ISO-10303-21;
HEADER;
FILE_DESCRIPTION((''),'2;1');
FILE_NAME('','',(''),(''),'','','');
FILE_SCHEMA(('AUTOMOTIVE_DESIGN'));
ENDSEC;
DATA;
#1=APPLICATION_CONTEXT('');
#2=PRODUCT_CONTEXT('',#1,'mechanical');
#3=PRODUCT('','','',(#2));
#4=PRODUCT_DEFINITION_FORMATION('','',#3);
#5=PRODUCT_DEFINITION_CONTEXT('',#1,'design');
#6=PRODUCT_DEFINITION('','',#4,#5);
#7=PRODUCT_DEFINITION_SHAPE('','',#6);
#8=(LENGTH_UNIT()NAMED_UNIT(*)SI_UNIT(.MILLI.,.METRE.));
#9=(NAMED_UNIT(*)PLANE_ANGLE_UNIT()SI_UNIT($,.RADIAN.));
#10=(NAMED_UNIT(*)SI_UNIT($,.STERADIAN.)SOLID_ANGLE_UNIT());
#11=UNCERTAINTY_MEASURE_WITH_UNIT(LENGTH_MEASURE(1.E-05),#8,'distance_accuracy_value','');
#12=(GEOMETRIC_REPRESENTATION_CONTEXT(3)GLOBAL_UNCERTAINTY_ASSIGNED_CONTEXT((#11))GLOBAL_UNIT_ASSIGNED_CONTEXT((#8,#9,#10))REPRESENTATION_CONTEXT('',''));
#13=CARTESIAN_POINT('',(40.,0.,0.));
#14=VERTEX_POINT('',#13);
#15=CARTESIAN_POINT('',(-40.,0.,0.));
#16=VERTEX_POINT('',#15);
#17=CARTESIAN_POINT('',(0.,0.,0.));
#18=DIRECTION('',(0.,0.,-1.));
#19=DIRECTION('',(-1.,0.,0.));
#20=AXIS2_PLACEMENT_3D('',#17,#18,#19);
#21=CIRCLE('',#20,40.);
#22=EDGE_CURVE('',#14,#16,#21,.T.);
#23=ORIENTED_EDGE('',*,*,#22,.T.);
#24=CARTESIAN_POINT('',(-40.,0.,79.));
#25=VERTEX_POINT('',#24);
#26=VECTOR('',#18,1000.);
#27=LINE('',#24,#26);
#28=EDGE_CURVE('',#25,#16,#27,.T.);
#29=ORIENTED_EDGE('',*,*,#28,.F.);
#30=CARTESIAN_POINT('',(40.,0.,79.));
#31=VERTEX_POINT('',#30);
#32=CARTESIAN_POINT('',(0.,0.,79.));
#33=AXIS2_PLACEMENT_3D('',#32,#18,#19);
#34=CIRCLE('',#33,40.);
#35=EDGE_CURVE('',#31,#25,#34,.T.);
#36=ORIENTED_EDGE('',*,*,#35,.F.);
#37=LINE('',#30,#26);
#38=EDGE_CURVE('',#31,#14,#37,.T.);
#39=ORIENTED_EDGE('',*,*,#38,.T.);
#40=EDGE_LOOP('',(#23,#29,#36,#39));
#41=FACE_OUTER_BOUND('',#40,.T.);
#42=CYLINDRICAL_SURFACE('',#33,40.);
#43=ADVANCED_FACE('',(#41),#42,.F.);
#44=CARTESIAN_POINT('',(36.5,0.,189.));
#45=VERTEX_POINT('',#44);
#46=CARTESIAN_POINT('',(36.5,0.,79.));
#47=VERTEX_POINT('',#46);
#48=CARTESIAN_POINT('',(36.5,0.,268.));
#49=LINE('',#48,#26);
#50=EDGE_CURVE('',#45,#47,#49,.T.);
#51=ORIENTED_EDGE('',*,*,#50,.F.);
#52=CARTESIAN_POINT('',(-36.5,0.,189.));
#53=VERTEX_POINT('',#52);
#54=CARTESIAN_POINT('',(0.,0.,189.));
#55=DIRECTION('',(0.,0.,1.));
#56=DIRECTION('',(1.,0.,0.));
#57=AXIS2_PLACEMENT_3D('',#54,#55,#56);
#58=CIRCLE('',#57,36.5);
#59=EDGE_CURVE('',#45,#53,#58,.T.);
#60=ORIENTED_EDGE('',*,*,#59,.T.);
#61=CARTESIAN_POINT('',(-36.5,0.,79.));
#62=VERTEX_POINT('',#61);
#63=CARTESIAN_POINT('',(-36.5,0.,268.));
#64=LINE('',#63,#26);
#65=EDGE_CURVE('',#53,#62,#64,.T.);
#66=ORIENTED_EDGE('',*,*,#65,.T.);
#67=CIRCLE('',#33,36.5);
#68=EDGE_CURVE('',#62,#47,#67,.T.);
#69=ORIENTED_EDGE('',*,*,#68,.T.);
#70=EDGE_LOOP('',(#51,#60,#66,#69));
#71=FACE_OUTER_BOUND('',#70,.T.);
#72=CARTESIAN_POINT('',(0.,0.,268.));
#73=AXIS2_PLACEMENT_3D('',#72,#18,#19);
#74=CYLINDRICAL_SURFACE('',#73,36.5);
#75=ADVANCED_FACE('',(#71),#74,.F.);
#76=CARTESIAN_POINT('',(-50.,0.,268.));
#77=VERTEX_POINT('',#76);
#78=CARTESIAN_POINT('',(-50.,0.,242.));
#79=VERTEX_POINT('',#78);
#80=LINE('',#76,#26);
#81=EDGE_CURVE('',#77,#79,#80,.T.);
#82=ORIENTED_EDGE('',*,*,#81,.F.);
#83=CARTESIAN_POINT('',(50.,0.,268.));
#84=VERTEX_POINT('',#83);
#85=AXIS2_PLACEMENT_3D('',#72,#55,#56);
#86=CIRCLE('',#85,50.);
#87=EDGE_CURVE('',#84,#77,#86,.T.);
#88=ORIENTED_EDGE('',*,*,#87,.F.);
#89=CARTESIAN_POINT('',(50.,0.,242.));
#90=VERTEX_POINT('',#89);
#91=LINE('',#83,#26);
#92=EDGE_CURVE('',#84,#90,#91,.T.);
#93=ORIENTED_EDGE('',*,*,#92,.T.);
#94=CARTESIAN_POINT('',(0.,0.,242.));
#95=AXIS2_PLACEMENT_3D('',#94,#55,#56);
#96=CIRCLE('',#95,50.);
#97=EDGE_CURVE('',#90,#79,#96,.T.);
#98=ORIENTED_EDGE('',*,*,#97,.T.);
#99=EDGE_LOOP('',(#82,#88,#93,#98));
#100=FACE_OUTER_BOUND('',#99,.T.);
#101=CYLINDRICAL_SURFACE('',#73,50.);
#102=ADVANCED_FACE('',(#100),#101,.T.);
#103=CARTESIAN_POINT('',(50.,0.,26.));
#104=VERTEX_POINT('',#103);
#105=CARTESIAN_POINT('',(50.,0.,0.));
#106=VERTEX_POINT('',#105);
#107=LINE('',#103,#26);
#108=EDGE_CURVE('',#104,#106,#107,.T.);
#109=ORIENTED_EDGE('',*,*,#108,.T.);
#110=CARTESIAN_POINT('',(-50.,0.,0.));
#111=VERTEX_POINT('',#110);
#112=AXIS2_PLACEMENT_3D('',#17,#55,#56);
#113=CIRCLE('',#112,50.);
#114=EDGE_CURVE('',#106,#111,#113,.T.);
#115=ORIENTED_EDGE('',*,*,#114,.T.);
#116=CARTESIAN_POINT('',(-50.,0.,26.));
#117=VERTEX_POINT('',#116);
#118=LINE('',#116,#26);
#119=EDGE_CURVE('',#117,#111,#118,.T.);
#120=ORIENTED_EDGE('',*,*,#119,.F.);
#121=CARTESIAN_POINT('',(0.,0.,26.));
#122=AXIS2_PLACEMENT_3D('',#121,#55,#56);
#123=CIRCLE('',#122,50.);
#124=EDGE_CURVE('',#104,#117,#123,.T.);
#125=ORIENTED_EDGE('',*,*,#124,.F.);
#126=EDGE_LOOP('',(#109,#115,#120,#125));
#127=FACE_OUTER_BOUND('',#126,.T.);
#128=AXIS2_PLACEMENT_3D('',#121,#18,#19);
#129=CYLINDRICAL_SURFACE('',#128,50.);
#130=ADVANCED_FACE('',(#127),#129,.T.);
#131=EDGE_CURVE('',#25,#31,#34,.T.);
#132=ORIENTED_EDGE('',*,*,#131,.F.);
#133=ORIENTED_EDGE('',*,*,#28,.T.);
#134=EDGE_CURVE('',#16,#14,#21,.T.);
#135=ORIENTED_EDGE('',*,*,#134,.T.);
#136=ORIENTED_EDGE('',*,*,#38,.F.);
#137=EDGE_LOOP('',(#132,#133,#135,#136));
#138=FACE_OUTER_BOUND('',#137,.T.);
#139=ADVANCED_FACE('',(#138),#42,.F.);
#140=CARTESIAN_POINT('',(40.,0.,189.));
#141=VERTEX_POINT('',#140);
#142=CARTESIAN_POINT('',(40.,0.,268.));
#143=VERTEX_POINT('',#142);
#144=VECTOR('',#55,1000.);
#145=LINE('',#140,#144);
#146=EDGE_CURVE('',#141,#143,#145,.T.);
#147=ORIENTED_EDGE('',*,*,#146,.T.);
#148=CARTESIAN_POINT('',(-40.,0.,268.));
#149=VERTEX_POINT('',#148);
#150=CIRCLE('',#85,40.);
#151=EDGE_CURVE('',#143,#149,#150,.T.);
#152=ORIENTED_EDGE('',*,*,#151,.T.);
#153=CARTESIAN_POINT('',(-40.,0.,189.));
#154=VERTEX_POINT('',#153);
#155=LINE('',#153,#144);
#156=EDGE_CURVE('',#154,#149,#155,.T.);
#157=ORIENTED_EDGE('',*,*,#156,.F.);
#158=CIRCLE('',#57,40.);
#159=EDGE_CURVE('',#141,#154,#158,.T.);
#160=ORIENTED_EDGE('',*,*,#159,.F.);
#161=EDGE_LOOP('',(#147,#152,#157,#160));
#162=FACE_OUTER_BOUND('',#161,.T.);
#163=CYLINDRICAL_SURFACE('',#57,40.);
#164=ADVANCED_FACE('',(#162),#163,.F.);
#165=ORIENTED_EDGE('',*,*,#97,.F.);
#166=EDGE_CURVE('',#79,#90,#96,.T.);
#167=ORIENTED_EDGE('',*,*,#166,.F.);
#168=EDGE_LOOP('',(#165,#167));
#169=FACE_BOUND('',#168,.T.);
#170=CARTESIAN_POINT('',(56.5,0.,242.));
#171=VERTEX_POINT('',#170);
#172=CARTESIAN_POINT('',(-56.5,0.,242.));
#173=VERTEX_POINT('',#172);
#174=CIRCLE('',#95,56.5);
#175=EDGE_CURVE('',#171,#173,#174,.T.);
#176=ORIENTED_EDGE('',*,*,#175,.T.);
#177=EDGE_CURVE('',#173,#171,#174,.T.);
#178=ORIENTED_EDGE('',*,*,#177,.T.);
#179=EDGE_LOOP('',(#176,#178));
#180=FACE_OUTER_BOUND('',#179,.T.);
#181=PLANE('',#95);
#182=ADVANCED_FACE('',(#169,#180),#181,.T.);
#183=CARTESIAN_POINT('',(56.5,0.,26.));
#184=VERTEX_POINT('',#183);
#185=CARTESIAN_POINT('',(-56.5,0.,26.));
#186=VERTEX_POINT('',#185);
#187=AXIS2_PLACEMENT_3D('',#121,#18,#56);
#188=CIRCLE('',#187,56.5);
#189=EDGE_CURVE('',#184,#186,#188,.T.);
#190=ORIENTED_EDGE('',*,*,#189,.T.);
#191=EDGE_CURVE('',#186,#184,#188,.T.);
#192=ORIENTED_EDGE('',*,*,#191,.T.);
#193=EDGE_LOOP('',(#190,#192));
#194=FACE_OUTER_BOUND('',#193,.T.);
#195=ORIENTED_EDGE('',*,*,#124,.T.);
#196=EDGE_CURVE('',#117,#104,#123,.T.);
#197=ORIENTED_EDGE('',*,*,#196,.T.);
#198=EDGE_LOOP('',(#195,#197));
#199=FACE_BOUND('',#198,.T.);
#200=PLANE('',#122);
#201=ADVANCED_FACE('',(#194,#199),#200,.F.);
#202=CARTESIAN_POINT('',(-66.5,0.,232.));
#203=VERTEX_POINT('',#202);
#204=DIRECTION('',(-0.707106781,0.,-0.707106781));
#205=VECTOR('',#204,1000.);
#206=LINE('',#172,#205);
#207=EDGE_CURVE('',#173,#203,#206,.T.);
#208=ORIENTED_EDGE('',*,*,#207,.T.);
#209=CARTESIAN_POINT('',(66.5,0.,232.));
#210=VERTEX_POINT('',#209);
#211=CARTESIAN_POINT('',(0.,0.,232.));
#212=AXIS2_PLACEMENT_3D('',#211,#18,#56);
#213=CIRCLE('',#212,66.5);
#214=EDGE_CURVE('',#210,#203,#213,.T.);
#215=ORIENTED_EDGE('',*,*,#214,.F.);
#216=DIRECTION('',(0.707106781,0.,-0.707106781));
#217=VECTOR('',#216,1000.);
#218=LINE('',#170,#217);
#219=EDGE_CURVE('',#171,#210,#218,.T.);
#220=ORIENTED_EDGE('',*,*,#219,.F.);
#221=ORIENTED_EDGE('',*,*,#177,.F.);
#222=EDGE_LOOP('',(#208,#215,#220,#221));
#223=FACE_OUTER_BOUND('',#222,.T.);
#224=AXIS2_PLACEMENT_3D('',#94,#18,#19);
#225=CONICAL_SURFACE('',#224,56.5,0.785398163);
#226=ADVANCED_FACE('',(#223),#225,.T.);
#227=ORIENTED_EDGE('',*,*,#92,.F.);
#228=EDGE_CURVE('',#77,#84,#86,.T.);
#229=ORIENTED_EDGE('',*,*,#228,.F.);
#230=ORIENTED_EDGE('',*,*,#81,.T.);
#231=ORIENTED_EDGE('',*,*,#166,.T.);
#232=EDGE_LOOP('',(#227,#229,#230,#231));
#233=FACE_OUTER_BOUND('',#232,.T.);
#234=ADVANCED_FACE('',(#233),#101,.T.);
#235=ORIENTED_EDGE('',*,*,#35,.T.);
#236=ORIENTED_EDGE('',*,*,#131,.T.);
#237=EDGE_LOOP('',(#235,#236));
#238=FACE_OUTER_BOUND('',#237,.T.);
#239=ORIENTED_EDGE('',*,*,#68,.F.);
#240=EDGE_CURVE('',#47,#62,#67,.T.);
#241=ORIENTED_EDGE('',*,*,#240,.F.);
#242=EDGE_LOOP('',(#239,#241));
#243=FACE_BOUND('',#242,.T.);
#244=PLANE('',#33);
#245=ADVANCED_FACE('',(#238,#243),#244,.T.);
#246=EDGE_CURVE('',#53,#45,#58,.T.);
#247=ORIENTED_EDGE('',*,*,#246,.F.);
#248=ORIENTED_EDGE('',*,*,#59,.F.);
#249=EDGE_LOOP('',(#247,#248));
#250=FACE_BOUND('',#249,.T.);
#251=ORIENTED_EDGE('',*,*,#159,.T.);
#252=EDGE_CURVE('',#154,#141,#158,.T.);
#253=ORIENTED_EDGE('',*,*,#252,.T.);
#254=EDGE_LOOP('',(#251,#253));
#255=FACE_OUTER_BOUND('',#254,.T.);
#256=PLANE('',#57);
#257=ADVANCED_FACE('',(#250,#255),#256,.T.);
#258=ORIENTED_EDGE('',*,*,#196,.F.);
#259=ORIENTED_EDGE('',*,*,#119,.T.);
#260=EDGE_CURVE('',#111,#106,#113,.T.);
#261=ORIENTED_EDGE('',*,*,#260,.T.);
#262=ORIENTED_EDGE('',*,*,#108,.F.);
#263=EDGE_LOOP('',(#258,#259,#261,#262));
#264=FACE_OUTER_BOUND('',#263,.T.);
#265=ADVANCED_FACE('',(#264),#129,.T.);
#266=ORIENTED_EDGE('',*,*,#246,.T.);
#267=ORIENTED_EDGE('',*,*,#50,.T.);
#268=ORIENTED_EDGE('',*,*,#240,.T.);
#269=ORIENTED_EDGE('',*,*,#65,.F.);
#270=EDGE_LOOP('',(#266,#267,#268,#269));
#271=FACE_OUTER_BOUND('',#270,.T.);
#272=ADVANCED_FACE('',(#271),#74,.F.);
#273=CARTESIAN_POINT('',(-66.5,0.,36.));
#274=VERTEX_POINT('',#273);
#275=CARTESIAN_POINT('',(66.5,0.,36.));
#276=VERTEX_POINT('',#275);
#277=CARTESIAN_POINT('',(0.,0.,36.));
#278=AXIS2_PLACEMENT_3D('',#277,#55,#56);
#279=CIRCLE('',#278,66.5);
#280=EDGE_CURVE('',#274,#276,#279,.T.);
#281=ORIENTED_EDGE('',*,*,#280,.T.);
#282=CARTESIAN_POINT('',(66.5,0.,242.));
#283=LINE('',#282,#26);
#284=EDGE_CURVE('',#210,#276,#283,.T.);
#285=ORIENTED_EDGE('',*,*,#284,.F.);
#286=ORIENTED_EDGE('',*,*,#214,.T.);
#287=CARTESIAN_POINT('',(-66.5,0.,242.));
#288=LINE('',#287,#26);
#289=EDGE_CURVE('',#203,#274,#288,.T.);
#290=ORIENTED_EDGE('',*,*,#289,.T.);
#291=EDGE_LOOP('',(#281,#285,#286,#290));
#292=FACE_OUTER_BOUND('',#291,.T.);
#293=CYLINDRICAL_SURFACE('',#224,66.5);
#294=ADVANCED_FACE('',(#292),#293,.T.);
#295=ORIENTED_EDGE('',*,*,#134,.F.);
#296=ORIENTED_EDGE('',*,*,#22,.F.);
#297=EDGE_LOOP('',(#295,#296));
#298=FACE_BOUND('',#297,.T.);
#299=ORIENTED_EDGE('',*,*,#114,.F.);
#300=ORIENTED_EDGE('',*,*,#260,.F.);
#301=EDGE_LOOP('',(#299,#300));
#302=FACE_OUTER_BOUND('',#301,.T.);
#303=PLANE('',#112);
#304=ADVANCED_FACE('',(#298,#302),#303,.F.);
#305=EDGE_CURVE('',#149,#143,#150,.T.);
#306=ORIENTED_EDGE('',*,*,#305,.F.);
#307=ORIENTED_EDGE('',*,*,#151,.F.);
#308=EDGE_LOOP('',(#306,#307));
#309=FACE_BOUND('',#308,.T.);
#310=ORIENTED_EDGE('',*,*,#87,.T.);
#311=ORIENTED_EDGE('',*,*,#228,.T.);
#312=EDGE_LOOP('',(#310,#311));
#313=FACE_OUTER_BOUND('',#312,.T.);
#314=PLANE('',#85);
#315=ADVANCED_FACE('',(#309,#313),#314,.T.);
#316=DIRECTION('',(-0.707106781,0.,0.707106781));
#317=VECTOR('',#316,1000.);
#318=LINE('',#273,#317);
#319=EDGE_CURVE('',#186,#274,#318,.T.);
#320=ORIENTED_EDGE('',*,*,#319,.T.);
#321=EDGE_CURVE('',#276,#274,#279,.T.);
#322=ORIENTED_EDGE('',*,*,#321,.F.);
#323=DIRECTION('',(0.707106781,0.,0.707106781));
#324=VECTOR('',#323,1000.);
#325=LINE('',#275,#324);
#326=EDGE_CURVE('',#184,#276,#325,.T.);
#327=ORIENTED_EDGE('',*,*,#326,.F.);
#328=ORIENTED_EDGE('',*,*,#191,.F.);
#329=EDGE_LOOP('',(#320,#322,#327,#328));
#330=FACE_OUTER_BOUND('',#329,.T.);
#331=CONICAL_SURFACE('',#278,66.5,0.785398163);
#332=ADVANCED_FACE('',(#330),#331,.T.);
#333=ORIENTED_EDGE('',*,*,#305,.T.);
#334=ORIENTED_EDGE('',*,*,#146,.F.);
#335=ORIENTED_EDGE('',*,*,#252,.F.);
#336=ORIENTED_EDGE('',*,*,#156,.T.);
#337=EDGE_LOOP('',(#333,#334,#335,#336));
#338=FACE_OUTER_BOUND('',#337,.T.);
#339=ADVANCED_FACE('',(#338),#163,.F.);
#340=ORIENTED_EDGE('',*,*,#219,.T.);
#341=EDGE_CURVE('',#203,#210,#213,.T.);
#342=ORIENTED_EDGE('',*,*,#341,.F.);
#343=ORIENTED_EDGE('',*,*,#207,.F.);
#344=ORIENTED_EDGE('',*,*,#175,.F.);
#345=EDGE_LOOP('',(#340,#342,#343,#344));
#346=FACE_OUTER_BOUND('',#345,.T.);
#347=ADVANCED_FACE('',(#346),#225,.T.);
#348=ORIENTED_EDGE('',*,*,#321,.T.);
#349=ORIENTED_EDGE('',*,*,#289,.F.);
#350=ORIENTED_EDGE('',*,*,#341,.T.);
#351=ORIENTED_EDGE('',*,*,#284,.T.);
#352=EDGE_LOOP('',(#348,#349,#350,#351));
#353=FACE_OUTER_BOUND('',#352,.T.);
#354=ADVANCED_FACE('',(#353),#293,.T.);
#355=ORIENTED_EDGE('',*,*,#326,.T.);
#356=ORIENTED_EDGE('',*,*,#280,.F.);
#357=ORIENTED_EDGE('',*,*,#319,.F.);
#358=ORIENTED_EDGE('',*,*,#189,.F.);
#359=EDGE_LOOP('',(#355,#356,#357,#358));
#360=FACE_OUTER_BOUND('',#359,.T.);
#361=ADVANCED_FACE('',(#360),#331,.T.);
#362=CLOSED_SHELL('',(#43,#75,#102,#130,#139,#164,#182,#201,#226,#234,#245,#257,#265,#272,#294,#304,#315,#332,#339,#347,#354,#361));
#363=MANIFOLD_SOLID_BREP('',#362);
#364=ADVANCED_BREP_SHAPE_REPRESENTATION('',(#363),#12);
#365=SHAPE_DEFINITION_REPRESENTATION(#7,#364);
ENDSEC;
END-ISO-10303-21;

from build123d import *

# Parameters (mm, degrees)
SKETCH1_R           = 50
BOSS_EXTRUDE1_DEPTH = 26
SKETCH2_R           = 66.5
BOSS_EXTRUDE2_DEPTH = 216
SKETCH3_R           = 50
BOSS_EXTRUDE3_DEPTH = 26
SKETCH4_R           = 40
CUT_EXTRUDE1_DEPTH  = 79
CUT_EXTRUDE2_START  = -79
SKETCH5_R           = 40
CUT_EXTRUDE2_DEPTH  = 79
SKETCH6_R           = 36.5
CUT_EXTRUDE3_DEPTH  = 212.1054239
CHAMFER1_SIZE       = 10
CHAMFER2_SIZE       = 10


with BuildPart() as part:
    # Sketch1 → Boss-Extrude1 (new body)
    with BuildSketch(Plane.XY):
        with Locations(Location((0, 0, 0), (0, 0, 180))):
            Circle(SKETCH1_R)
    extrude(amount=BOSS_EXTRUDE1_DEPTH)

    # Sketch2 → Boss-Extrude2 (add)
    with BuildSketch(Plane.XY.offset(26)):
        Circle(SKETCH2_R)
    extrude(amount=BOSS_EXTRUDE2_DEPTH)

    # Sketch3 → Boss-Extrude3 (add)
    with BuildSketch(Plane.XY.offset(242)):
        with Locations(Location((0, 0, 0), (0, 0, 180))):
            Circle(SKETCH3_R)
    extrude(amount=BOSS_EXTRUDE3_DEPTH)

    # Sketch4 → Cut-Extrude1 (cut)
    with BuildSketch(Plane.XY.offset(268)):
        Circle(SKETCH4_R)
    extrude(amount=-CUT_EXTRUDE1_DEPTH, mode=Mode.SUBTRACT)

    # Sketch5 → Cut-Extrude2 (cut)
    with BuildSketch(Plane(origin=(0, 0, 0), x_dir=(-1, 0, 0), z_dir=(0, 0, -1)).offset(CUT_EXTRUDE2_START)):
        with Locations(Location((0, 0, 0), (0, 0, 180))):
            Circle(SKETCH5_R)
    extrude(amount=CUT_EXTRUDE2_DEPTH, mode=Mode.SUBTRACT)

    # Sketch6 → Cut-Extrude3 (cut, through all)
    with BuildSketch(Plane(origin=(0, 0, 79), x_dir=(-1, 0, 0), z_dir=(0, 0, -1))):
        Circle(SKETCH6_R)
    extrude(amount=-CUT_EXTRUDE3_DEPTH, mode=Mode.SUBTRACT)

    # Chamfer1
    chamfer1_edges = [part.edges().sort_by_distance(p)[0] for p in [
        (-66.5, 0, 242),
    ]]
    chamfer(chamfer1_edges, length=CHAMFER1_SIZE)

    # Chamfer2
    chamfer2_edges = [part.edges().sort_by_distance(p)[0] for p in [
        (-66.5, 0, 26),
    ]]
    chamfer(chamfer2_edges, length=CHAMFER2_SIZE)


solid = part.part
